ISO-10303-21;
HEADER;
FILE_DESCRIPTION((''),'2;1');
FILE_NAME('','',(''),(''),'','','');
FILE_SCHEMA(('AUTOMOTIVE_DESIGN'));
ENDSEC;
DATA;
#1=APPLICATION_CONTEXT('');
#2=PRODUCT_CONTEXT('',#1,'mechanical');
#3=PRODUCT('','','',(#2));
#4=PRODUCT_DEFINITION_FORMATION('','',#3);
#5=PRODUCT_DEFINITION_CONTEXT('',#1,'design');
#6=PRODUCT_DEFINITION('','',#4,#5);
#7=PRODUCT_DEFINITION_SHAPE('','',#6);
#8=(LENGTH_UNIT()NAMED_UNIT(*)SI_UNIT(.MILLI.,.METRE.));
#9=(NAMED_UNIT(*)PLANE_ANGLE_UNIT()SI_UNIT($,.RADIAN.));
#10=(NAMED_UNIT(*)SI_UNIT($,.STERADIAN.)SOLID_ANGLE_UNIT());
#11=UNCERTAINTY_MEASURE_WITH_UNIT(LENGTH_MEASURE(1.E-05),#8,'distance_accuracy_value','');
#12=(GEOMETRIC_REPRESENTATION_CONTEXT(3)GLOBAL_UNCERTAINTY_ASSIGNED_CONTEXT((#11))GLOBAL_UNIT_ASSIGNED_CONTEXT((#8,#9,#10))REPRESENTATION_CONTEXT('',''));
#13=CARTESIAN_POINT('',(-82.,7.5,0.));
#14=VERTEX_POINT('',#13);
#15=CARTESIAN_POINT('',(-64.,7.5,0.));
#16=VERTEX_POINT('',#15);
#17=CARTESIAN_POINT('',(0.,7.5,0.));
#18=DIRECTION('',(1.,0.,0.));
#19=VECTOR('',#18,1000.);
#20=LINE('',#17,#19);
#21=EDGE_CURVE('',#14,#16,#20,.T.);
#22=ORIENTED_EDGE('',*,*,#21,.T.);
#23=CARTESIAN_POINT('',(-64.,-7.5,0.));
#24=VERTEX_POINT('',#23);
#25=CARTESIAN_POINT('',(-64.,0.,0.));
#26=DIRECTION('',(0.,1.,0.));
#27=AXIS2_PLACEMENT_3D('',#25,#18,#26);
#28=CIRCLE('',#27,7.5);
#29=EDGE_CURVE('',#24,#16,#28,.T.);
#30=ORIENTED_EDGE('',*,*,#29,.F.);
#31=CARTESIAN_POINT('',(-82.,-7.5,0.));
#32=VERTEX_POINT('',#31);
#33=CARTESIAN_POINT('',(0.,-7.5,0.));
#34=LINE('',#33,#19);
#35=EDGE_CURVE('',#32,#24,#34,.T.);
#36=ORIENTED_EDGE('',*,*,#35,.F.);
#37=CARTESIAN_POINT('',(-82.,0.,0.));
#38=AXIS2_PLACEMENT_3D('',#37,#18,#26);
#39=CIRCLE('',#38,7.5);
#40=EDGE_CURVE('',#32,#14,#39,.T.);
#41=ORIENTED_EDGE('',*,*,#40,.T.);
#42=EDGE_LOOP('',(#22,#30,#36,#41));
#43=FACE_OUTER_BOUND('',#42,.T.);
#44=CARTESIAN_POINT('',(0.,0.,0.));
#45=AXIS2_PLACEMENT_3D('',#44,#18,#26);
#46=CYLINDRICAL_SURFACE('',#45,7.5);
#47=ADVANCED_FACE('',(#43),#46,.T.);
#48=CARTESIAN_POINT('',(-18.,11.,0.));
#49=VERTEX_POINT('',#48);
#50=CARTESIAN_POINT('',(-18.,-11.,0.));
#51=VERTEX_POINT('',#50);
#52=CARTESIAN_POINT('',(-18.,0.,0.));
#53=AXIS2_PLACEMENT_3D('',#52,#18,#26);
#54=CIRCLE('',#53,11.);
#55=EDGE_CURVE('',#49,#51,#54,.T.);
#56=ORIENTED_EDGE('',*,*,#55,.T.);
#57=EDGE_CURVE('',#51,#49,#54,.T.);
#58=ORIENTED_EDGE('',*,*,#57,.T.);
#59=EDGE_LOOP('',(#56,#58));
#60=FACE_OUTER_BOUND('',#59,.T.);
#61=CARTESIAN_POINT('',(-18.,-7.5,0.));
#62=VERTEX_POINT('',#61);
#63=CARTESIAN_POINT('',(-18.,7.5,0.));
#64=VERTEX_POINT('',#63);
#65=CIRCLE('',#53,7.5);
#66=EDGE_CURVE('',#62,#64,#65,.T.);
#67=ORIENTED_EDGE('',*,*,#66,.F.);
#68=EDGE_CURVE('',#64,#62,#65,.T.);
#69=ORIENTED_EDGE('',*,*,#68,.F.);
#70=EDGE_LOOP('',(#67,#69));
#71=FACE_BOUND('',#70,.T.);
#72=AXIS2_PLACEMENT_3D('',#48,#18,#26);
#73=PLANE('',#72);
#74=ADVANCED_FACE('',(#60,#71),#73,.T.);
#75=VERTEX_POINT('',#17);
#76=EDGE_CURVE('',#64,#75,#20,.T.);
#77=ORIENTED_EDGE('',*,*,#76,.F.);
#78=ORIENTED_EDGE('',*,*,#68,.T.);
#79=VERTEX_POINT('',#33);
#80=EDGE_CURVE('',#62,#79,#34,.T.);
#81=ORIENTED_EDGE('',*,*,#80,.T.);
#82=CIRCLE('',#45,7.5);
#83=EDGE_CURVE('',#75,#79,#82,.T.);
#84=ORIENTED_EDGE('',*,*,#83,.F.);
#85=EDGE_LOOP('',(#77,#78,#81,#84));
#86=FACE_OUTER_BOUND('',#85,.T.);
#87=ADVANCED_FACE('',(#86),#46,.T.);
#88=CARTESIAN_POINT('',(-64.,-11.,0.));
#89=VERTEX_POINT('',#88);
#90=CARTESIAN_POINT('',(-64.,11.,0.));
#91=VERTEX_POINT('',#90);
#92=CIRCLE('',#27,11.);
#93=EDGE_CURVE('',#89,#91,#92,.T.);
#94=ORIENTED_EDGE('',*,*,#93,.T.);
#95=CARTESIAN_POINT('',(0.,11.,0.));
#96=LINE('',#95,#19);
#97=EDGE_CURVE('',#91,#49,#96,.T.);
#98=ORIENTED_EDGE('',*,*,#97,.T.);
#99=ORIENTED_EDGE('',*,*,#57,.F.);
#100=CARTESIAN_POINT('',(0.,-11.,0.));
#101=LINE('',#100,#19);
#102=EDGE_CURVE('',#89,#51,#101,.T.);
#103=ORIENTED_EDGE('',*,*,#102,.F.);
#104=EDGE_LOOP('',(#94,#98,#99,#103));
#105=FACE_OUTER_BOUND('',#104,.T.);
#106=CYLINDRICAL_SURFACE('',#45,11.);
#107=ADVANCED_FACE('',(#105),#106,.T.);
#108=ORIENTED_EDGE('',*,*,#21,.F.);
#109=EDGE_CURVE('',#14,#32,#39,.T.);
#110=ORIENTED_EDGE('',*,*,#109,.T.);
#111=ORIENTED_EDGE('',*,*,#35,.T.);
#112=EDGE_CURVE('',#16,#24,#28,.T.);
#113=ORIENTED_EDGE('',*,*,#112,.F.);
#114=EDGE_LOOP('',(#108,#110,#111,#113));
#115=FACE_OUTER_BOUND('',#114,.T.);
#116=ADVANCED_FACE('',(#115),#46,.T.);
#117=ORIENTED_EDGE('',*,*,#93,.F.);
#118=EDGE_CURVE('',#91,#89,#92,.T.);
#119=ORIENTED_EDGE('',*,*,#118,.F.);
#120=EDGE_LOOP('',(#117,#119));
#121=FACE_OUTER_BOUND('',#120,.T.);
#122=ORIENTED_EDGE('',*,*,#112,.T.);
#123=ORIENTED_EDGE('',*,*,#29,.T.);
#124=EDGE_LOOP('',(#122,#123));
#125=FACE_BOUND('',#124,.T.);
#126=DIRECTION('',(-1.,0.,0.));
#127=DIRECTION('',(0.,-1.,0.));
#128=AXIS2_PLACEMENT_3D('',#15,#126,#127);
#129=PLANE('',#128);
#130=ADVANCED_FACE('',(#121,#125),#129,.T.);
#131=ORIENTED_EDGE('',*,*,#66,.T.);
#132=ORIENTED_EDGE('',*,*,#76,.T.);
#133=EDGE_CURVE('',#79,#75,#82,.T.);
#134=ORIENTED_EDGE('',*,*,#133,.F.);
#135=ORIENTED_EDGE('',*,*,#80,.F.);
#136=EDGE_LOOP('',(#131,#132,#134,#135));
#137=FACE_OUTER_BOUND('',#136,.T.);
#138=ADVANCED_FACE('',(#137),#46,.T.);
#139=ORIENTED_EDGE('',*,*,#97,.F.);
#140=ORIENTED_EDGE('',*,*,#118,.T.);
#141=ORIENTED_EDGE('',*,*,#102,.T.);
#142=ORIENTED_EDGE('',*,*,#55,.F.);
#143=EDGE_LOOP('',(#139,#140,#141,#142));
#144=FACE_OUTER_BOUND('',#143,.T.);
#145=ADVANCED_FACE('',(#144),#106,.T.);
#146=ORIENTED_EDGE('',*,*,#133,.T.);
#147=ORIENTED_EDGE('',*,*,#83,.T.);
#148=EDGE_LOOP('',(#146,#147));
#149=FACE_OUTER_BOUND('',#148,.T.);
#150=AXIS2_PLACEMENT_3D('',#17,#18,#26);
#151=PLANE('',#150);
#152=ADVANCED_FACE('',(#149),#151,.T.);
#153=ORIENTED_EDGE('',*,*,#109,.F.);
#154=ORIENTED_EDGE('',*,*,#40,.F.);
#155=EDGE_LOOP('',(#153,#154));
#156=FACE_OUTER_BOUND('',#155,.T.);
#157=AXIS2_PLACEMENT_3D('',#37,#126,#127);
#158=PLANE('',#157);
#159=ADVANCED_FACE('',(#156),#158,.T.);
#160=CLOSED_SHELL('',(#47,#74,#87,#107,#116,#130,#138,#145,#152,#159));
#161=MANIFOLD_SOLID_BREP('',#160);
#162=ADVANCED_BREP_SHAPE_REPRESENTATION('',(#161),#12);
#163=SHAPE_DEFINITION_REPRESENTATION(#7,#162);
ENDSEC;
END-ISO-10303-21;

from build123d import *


with BuildPart() as part:
    # Spacer Profile Sketch → Spacer Body Revolve (revolve)
    with BuildSketch(Plane.XY):
        Polygon((-82, 0), (-82, 7.5), (-64, 7.5), (-64, 11), (-18, 11), (-18, 7.5), (0, 7.5), (0, 0), align=None)
    revolve(axis=Axis((0, 0, 0), (-1, 0, 0)))


solid = part.part
